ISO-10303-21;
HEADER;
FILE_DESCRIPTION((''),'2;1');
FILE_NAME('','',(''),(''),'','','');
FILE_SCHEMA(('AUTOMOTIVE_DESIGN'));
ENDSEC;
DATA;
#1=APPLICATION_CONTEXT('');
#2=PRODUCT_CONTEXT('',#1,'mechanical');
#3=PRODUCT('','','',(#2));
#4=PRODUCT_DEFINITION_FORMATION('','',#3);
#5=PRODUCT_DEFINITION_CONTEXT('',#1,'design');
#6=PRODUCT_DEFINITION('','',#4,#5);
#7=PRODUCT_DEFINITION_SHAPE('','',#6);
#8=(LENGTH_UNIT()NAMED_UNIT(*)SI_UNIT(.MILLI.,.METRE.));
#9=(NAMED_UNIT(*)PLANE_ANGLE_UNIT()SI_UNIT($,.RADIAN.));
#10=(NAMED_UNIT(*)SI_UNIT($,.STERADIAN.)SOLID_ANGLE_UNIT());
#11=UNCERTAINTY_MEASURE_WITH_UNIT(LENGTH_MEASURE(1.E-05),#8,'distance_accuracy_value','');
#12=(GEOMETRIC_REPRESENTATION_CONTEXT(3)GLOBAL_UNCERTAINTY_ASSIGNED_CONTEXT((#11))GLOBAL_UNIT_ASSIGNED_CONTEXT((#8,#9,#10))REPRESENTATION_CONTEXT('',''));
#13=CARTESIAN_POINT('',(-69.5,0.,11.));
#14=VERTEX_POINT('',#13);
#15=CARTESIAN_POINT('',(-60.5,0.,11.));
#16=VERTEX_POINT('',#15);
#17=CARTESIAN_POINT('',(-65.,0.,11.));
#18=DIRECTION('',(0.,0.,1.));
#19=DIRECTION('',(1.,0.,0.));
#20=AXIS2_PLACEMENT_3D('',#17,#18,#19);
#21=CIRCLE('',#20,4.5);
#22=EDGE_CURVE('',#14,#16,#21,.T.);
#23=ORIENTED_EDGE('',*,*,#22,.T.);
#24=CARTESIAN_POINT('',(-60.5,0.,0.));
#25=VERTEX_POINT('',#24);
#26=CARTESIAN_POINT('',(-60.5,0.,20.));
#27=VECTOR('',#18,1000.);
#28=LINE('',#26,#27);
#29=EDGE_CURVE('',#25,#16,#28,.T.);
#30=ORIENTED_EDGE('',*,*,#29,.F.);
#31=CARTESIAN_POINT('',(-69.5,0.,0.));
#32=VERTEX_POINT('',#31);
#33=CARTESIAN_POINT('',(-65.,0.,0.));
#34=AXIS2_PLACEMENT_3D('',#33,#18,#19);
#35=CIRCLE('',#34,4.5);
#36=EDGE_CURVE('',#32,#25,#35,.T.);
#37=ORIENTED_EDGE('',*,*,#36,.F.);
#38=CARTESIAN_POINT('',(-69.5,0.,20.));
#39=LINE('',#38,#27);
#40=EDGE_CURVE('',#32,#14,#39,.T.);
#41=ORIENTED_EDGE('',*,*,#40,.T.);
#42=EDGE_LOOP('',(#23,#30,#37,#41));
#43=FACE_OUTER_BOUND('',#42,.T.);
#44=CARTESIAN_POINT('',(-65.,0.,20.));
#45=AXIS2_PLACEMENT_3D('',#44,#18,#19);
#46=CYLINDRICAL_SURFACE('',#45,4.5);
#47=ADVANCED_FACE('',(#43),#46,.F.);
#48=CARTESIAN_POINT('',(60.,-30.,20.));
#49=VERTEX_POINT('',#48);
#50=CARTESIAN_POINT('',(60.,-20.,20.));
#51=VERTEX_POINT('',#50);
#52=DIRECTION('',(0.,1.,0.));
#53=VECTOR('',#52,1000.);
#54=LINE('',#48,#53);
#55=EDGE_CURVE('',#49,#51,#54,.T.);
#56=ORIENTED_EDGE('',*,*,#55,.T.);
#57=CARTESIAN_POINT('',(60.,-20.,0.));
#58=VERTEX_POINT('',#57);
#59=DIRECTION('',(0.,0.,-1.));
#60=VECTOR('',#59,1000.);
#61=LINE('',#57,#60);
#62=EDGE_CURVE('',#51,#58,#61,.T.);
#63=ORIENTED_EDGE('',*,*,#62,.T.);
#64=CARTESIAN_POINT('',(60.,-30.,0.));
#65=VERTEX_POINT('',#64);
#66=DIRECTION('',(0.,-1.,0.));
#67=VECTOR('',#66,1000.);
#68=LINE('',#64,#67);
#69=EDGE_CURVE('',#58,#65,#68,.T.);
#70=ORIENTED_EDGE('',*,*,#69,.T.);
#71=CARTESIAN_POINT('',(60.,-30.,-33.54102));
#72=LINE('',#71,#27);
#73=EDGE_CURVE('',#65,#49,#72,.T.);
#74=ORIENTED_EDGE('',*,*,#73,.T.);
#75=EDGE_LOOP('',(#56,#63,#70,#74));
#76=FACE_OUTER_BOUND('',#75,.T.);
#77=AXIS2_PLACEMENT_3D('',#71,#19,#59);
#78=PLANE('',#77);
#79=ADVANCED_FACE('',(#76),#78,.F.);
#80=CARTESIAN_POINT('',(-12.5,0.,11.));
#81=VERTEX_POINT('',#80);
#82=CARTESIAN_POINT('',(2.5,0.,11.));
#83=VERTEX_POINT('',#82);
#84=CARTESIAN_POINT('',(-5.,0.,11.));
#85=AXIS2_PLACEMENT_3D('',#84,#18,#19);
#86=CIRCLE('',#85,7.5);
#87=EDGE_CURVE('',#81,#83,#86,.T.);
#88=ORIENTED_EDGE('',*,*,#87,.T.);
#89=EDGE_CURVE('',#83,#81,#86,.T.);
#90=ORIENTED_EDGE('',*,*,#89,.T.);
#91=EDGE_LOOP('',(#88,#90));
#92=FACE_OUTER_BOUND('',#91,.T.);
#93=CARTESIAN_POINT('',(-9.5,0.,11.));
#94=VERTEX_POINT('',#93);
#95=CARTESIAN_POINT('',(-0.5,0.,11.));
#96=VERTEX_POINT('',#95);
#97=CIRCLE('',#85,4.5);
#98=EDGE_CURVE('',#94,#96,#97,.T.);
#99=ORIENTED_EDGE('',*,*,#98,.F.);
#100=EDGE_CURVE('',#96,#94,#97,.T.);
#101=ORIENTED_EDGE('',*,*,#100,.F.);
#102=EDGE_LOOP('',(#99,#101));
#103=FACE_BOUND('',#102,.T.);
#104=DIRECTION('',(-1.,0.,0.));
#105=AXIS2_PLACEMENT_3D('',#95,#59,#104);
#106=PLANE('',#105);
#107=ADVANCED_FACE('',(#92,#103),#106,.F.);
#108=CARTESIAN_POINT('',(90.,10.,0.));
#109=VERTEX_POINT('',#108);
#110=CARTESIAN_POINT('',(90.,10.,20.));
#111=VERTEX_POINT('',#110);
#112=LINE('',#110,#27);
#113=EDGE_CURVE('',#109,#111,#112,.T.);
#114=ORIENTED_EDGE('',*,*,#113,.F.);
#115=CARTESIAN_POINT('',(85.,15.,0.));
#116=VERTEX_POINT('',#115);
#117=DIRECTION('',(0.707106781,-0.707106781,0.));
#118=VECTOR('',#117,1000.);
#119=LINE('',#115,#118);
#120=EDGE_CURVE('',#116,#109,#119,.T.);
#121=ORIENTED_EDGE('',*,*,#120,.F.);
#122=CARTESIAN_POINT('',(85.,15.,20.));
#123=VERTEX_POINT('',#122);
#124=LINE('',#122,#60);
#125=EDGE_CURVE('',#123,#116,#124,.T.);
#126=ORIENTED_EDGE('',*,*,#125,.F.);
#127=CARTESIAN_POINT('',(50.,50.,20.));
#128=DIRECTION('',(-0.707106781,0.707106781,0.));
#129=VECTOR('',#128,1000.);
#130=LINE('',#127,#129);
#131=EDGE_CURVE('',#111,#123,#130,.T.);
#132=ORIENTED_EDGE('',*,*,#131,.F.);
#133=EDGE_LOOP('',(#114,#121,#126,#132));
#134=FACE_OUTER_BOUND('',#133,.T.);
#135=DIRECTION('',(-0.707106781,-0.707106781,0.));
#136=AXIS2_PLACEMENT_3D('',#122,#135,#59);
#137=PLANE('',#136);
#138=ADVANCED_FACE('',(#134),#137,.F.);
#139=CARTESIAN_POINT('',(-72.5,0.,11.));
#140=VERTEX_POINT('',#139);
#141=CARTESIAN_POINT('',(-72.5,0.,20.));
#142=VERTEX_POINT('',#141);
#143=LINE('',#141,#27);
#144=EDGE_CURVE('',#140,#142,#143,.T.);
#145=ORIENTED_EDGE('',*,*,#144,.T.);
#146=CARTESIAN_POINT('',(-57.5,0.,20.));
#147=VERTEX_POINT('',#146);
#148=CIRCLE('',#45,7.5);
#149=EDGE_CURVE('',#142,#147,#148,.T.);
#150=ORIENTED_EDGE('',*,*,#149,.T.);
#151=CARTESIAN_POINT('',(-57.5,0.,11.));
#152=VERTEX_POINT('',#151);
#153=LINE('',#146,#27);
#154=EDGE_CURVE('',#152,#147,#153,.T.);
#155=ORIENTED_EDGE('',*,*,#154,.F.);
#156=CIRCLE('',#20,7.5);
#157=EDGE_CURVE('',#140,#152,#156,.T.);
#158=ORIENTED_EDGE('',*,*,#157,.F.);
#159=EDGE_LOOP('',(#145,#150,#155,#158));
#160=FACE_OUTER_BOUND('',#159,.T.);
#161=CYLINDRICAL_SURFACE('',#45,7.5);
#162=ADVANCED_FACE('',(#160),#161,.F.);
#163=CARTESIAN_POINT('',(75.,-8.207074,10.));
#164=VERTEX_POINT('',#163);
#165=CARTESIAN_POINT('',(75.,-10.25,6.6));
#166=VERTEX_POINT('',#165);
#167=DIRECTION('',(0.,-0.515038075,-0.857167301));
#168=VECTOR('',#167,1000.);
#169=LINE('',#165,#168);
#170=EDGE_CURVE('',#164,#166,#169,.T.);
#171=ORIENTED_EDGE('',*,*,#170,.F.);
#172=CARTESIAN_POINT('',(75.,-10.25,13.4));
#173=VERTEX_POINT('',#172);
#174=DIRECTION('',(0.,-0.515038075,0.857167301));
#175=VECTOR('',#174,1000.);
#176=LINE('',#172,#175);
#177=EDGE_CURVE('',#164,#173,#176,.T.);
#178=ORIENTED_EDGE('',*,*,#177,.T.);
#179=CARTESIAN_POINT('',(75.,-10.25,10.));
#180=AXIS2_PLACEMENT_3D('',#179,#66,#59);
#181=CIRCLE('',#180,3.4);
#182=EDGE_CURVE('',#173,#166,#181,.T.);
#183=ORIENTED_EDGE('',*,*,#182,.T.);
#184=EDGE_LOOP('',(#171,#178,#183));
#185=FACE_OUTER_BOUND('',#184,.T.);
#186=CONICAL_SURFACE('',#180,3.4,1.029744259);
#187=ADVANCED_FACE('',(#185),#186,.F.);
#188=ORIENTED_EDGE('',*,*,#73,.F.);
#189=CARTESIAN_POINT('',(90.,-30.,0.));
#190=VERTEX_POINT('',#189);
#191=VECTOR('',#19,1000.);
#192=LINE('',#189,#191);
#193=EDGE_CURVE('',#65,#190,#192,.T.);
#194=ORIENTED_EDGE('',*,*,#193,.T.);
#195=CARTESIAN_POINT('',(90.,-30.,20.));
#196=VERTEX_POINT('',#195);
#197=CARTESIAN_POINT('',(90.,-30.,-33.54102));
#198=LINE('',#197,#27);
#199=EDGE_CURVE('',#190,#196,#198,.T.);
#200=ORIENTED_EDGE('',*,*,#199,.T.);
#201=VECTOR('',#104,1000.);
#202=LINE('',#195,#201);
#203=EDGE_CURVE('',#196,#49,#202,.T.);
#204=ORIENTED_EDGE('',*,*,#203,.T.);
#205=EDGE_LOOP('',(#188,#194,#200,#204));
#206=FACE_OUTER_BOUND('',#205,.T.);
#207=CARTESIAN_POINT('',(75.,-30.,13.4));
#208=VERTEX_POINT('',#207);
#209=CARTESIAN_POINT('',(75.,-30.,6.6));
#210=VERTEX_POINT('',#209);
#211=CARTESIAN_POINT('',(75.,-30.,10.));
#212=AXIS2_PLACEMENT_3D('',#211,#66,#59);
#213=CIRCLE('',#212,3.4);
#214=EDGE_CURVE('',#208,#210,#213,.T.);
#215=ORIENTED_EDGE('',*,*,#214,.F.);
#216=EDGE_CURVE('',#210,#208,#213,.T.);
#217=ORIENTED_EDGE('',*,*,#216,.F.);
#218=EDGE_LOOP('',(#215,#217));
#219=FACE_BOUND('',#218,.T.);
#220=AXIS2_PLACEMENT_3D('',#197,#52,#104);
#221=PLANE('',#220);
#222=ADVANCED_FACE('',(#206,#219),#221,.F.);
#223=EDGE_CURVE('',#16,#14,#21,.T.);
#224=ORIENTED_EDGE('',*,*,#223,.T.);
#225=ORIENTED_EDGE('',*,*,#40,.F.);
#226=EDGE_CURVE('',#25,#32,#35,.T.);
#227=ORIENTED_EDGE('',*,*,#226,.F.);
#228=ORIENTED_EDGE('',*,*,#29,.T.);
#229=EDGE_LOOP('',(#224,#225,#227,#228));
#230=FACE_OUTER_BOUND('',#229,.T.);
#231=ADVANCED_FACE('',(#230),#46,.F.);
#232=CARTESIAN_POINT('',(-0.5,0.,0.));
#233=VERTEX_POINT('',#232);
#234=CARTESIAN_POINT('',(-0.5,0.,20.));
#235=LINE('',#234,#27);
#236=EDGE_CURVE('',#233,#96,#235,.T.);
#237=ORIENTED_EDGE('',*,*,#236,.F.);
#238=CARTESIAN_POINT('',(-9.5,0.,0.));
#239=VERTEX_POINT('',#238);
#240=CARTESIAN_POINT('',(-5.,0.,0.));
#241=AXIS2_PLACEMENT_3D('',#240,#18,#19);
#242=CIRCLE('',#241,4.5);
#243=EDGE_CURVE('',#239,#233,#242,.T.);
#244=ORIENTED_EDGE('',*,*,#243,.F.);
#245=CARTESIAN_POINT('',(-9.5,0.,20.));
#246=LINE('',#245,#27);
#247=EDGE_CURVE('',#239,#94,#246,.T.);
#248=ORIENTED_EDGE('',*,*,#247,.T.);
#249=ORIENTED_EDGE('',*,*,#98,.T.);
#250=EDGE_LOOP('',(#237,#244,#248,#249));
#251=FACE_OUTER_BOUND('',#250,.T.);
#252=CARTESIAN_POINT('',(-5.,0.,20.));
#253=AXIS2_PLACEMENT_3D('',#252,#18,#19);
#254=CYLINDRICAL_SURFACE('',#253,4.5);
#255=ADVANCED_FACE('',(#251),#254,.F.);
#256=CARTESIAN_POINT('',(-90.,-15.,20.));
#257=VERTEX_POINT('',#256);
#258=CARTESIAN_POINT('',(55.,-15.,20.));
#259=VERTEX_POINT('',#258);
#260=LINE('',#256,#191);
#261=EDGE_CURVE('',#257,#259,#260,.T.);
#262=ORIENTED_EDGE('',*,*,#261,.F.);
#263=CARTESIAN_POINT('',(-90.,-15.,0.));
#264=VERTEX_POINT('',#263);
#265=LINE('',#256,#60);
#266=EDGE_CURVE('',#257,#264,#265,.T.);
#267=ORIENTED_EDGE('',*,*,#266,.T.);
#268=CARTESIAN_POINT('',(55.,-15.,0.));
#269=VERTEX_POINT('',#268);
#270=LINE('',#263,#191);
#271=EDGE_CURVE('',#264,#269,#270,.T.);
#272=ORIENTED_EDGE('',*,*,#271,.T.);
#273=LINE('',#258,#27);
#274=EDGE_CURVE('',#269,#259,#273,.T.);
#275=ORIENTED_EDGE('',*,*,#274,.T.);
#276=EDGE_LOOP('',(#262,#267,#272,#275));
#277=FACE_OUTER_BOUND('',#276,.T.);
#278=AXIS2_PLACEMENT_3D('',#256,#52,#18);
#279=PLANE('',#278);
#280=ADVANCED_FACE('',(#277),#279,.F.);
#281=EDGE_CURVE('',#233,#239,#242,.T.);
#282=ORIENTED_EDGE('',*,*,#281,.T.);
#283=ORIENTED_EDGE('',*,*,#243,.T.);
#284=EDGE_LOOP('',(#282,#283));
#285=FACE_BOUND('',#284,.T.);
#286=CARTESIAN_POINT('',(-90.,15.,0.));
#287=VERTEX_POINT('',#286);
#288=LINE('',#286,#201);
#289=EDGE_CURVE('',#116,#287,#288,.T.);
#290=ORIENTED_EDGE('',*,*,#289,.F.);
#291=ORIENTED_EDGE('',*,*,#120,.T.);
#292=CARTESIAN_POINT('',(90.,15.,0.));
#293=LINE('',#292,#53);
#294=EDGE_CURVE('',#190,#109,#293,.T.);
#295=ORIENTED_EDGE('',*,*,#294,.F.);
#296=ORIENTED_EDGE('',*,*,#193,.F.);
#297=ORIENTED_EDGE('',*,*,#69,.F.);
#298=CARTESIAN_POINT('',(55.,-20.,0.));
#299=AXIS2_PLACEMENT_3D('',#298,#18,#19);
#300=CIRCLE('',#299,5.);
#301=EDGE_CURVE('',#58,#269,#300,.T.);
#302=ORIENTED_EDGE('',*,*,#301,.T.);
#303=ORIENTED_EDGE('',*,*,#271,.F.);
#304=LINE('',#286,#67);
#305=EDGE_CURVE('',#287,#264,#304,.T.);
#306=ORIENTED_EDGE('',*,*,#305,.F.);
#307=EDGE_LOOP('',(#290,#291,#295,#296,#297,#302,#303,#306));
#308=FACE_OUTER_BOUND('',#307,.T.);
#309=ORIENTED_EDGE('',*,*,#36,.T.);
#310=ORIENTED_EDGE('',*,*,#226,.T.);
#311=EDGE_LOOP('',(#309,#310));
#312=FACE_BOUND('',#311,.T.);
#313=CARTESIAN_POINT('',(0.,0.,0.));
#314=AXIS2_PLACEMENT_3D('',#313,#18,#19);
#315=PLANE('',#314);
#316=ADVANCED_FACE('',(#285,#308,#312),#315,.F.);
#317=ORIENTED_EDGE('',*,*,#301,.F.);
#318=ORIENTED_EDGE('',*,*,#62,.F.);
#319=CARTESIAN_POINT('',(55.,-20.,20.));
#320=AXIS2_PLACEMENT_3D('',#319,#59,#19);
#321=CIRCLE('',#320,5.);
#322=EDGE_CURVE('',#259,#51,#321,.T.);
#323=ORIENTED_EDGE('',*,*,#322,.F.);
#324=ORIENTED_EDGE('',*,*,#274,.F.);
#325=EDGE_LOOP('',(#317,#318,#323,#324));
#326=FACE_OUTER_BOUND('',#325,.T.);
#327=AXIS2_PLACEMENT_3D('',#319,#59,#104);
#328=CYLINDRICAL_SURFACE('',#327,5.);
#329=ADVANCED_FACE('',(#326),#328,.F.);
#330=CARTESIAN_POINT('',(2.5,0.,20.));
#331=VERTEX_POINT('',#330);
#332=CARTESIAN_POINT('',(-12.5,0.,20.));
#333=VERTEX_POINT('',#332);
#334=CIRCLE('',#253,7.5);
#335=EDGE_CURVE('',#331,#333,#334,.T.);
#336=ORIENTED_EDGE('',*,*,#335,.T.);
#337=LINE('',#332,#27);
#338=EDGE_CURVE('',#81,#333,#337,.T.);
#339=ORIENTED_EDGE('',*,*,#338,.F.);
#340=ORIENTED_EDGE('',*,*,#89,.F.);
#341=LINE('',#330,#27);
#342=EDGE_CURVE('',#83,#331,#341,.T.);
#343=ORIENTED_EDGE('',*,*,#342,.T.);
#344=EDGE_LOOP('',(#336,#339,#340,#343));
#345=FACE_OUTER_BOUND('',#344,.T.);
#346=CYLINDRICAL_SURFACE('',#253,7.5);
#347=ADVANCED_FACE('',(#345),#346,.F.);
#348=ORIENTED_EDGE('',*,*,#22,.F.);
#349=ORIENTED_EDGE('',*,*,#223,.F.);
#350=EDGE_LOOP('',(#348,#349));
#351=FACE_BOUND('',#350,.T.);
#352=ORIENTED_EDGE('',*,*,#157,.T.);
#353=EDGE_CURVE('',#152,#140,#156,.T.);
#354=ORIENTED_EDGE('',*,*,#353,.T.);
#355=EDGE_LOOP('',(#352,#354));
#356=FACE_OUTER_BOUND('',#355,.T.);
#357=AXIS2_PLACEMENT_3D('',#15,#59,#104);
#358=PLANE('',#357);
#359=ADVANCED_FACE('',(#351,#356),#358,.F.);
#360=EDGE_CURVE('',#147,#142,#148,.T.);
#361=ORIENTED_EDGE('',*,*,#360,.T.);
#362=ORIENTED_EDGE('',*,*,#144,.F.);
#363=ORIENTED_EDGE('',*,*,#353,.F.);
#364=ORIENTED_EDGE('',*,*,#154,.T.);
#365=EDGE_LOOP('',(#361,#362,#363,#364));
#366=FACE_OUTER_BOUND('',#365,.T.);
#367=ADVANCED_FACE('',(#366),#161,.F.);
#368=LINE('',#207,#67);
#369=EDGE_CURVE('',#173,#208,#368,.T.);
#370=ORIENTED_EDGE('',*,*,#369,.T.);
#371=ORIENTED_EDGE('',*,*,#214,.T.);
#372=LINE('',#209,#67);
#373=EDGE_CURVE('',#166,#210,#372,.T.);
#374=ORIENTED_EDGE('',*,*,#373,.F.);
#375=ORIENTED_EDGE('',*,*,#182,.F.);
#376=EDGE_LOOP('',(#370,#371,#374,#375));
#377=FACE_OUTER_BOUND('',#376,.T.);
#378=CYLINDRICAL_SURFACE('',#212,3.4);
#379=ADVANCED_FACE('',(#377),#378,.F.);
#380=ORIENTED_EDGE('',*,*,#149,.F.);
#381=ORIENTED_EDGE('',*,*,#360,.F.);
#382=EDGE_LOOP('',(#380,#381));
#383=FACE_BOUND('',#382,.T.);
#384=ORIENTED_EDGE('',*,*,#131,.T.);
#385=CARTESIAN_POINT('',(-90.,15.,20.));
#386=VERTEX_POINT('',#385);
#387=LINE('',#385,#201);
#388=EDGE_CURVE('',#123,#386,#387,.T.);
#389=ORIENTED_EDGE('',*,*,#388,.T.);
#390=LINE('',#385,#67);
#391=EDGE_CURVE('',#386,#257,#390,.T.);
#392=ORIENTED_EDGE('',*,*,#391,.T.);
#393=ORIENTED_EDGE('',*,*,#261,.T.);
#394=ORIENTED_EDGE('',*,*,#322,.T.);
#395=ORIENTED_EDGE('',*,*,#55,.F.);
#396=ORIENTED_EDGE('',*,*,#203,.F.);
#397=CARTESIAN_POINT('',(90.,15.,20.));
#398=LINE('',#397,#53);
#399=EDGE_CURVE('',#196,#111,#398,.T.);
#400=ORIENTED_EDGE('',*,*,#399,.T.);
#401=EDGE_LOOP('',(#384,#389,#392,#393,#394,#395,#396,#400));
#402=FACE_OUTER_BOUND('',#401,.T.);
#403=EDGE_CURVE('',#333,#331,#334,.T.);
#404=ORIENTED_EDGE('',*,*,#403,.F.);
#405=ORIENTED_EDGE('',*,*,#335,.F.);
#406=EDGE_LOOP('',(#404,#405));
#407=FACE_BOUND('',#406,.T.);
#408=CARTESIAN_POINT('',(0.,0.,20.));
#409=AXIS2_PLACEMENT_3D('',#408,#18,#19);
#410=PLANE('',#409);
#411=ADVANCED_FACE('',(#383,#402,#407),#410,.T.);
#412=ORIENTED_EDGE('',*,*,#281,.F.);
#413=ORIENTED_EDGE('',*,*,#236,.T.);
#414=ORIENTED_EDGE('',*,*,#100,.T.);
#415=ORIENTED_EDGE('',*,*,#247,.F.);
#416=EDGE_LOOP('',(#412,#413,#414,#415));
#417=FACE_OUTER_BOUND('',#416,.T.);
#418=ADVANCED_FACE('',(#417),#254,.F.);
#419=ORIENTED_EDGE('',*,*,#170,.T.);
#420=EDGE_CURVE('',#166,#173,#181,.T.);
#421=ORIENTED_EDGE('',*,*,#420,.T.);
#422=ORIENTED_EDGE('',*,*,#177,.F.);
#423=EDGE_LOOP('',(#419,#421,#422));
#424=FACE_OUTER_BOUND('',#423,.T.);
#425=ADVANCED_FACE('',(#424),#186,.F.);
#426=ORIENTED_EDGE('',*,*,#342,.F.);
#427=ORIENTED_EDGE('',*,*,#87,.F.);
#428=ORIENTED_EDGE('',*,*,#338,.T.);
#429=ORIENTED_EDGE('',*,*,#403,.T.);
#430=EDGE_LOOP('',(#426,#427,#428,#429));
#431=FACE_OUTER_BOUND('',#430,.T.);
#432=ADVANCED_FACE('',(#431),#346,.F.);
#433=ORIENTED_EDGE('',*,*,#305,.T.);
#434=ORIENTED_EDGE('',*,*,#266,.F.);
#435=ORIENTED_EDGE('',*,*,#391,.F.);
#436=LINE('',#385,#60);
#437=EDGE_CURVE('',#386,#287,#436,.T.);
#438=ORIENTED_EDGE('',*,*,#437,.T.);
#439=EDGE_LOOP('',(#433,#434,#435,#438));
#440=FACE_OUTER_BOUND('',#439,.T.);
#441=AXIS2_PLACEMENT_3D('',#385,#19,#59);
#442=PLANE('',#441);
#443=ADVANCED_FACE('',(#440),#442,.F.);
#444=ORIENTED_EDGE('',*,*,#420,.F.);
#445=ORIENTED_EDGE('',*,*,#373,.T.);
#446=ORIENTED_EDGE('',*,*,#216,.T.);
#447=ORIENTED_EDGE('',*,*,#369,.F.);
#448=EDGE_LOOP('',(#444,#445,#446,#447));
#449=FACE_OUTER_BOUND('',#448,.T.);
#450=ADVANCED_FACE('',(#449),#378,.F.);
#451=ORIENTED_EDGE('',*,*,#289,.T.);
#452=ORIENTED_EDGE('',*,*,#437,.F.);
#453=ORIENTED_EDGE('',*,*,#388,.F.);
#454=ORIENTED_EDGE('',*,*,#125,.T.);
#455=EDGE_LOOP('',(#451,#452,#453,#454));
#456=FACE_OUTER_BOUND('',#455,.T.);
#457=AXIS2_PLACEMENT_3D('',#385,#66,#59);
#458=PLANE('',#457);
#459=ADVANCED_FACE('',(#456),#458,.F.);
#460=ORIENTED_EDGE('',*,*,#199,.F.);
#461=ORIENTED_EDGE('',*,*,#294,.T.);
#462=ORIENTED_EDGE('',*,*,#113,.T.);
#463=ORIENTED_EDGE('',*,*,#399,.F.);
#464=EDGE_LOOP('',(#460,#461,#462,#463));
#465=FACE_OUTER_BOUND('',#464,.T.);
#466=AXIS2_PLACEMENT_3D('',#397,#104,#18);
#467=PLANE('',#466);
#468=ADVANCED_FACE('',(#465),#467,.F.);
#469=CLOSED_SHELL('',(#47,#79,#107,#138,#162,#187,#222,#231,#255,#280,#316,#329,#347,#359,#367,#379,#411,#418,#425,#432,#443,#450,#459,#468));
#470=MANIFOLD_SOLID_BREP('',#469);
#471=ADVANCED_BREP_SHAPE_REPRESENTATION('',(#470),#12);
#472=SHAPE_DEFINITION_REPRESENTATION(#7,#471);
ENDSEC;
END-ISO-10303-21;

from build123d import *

# Parameters (mm, degrees)
SKETCH_1_W                = 180
SKETCH_1_H                = 30
EXTRUDE_1_DEPTH           = 20
HOLE_WIZARD_1_D           = 9
HOLE_WIZARD_1_CBORE_D     = 15
HOLE_WIZARD_1_CBORE_DEPTH = 9
SKETCH_4_W                = 30
SKETCH_4_H                = 15
EXTRUDE_2_DEPTH           = 20
FILLET_1_R                = 5
CHAMFER_1_SIZE            = 5
HOLE_WIZARD_M8_2_D        = 6.8
HOLE_WIZARD_M8_2_DEPTH    = 19.75
HOLE_WIZARD_M8_2_TIP      = 2.042926105


with BuildPart() as part:
    # 草图1 → 凸台-拉伸1 (new body)
    with BuildSketch(Plane.XY):
        Rectangle(SKETCH_1_W, SKETCH_1_H)
    extrude(amount=EXTRUDE_1_DEPTH)

    # 打孔尺寸(%根据)内六角圆柱头螺钉的类型1 (through all)
    with Locations(Plane.XY.offset(20)):
        with Locations((-65, 0), (-5, 0)):
            CounterBoreHole(HOLE_WIZARD_1_D / 2, HOLE_WIZARD_1_CBORE_D / 2, HOLE_WIZARD_1_CBORE_DEPTH)

    # 草图4 → 凸台-拉伸2 (add)
    with BuildSketch(Plane.XY.offset(20)):
        with Locations((75, -22.5)):
            Rectangle(SKETCH_4_W, SKETCH_4_H)
    extrude(amount=-EXTRUDE_2_DEPTH)

    # 圆角1
    fillet_1_edges = [part.edges().sort_by_distance(p)[0] for p in [
        (60, -15, 10),
    ]]
    fillet(fillet_1_edges, radius=FILLET_1_R)

    # 倒角1
    chamfer_1_edges = [part.edges().sort_by_distance(p)[0] for p in [
        (90, 15, 10),
    ]]
    chamfer(chamfer_1_edges, length=CHAMFER_1_SIZE)

    # M8 螺纹孔2
    with Locations(Plane(origin=(0, -30, 0), x_dir=(-1, 0, 0), z_dir=(0, -1, 0))):
        with Locations((-75, -10)):
            Hole(HOLE_WIZARD_M8_2_D / 2, depth=HOLE_WIZARD_M8_2_DEPTH)
            with Locations((0, 0, -(HOLE_WIZARD_M8_2_DEPTH + HOLE_WIZARD_M8_2_TIP / 2))):  # 118° drill point
                Cone(0, HOLE_WIZARD_M8_2_D / 2, HOLE_WIZARD_M8_2_TIP, mode=Mode.SUBTRACT)


solid = part.part
